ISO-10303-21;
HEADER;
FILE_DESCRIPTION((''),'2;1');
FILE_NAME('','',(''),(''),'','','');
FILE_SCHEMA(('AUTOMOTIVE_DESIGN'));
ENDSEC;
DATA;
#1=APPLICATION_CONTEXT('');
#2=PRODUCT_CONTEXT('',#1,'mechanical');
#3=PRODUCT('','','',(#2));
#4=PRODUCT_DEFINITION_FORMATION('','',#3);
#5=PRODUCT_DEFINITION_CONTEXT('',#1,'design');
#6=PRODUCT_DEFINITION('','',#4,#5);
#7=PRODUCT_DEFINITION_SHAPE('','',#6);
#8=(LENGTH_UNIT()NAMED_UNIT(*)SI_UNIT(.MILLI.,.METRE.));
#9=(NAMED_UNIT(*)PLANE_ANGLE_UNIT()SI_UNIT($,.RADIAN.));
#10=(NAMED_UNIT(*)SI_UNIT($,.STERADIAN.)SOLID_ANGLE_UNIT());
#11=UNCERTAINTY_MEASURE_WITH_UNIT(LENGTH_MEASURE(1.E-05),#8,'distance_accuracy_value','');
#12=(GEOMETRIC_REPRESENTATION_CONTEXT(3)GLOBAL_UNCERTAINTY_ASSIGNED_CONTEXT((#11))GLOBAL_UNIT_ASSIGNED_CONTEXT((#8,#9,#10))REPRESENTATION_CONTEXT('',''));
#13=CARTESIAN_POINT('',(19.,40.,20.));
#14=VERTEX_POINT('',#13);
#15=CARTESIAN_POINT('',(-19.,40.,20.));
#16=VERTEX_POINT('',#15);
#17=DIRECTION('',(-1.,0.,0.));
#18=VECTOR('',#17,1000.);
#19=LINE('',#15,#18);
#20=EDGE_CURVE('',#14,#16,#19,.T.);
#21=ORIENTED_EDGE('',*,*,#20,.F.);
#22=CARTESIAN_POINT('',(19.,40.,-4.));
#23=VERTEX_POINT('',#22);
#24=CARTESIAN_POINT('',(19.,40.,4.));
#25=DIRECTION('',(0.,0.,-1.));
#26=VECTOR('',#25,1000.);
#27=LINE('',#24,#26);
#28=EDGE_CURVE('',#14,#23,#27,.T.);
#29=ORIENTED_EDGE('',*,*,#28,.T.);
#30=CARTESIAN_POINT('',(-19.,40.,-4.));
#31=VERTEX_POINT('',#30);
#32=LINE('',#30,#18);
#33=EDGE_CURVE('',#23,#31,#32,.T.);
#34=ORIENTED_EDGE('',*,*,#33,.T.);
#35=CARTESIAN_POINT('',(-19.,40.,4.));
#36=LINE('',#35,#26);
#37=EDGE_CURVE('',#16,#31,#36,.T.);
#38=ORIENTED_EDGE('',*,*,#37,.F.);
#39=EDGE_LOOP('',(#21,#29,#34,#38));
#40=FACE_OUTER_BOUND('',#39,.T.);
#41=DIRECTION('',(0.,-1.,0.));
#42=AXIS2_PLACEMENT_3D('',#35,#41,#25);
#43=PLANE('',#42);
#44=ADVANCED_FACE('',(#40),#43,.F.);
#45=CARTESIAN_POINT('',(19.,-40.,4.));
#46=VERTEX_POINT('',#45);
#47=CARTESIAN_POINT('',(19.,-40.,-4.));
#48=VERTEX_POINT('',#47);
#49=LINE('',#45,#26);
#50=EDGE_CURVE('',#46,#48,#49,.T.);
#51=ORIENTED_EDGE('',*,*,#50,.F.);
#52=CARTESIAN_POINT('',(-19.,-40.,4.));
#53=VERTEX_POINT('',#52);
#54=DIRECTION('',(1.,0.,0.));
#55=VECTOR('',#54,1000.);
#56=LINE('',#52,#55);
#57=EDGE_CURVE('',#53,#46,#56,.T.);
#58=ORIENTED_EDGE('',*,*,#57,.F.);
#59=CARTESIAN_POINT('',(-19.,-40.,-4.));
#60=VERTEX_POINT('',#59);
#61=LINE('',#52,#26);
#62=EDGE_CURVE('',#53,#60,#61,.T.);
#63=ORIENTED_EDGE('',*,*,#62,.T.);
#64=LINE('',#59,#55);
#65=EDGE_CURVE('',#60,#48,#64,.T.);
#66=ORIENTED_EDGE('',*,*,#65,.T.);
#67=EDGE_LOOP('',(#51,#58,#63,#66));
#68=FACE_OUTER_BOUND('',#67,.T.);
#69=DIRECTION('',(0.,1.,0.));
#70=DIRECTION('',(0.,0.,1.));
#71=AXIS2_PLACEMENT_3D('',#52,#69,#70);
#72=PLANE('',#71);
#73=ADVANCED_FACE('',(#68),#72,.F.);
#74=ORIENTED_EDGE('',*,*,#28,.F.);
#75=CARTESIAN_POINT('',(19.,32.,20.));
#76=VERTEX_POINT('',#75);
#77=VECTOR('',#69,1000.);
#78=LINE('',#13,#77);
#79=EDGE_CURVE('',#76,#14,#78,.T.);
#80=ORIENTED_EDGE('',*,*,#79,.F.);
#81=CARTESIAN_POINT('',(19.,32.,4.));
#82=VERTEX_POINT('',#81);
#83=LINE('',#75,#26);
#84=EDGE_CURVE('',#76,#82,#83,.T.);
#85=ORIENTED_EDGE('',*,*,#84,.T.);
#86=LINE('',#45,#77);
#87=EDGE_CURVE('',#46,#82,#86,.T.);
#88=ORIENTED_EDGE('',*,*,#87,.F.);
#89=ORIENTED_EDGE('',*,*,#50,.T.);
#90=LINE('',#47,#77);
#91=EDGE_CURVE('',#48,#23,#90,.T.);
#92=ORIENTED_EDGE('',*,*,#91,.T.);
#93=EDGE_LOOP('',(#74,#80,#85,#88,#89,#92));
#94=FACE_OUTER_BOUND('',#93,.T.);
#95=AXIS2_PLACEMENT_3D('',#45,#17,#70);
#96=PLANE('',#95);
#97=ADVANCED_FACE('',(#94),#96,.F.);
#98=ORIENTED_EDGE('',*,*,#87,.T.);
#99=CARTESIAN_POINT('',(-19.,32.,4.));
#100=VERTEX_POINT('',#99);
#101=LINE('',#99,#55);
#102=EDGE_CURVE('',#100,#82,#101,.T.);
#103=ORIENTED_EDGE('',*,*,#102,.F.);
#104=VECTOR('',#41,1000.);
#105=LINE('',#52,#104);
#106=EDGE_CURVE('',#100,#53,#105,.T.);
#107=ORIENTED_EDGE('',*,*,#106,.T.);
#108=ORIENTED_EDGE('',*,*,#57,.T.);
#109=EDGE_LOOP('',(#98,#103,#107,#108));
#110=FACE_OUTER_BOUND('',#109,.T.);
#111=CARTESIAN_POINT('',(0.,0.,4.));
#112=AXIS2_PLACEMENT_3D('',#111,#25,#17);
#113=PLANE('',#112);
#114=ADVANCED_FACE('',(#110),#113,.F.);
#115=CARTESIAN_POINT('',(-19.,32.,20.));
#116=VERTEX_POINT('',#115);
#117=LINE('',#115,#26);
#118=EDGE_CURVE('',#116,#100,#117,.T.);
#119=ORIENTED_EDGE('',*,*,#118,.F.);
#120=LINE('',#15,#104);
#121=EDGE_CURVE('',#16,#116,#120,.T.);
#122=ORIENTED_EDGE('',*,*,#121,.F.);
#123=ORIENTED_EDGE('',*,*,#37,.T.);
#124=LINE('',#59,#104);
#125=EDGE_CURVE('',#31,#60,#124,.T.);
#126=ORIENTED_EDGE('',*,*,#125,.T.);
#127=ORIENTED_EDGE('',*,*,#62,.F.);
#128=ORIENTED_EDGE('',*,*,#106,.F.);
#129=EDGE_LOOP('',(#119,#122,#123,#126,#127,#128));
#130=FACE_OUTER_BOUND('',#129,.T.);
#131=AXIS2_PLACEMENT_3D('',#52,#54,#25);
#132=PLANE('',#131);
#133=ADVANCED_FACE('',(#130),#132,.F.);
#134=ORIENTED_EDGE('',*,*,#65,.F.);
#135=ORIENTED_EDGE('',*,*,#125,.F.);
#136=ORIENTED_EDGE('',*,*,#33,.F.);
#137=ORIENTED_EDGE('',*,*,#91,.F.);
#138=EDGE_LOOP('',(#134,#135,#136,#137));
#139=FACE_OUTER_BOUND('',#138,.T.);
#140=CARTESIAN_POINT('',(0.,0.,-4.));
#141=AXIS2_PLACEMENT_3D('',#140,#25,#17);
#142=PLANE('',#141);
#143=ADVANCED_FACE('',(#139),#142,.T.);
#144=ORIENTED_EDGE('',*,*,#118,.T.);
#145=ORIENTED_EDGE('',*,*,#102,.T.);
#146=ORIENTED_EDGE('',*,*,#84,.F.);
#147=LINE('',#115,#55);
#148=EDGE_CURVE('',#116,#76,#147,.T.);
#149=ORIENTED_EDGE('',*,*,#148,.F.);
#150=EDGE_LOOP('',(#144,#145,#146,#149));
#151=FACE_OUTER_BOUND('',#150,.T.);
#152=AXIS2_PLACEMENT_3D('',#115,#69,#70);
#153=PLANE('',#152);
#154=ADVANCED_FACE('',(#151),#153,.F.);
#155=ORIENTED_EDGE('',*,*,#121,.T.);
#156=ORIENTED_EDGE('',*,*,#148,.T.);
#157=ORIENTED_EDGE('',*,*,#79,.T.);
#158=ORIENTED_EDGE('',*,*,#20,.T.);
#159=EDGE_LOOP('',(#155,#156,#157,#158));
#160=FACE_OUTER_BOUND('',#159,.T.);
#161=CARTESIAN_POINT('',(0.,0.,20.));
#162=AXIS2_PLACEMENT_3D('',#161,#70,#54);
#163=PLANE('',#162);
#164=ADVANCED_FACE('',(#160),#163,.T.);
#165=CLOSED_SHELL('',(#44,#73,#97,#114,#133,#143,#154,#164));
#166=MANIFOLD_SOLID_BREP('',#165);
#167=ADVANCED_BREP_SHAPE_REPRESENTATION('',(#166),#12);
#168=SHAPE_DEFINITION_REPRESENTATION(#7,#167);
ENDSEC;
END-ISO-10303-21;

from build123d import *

# Parameters (mm, degrees)
SKETCH_1_W      = 38
SKETCH_1_H      = 80
EXTRUDE_1_DEPTH = 4
SKETCH_2_W      = 38
SKETCH_2_H      = 8
EXTRUDE_2_DEPTH = 16


with BuildPart() as part:
    # 草图1 → 凸台-拉伸1 (new, symmetric)
    with BuildSketch(Plane.XY):
        Rectangle(SKETCH_1_W, SKETCH_1_H)
    extrude(amount=EXTRUDE_1_DEPTH, both=True)

    # 草图2 → 凸台-拉伸2 (add)
    with BuildSketch(Plane.XY.offset(4)):
        with Locations((0, 36)):
            Rectangle(SKETCH_2_W, SKETCH_2_H)
    extrude(amount=EXTRUDE_2_DEPTH)


solid = part.part
